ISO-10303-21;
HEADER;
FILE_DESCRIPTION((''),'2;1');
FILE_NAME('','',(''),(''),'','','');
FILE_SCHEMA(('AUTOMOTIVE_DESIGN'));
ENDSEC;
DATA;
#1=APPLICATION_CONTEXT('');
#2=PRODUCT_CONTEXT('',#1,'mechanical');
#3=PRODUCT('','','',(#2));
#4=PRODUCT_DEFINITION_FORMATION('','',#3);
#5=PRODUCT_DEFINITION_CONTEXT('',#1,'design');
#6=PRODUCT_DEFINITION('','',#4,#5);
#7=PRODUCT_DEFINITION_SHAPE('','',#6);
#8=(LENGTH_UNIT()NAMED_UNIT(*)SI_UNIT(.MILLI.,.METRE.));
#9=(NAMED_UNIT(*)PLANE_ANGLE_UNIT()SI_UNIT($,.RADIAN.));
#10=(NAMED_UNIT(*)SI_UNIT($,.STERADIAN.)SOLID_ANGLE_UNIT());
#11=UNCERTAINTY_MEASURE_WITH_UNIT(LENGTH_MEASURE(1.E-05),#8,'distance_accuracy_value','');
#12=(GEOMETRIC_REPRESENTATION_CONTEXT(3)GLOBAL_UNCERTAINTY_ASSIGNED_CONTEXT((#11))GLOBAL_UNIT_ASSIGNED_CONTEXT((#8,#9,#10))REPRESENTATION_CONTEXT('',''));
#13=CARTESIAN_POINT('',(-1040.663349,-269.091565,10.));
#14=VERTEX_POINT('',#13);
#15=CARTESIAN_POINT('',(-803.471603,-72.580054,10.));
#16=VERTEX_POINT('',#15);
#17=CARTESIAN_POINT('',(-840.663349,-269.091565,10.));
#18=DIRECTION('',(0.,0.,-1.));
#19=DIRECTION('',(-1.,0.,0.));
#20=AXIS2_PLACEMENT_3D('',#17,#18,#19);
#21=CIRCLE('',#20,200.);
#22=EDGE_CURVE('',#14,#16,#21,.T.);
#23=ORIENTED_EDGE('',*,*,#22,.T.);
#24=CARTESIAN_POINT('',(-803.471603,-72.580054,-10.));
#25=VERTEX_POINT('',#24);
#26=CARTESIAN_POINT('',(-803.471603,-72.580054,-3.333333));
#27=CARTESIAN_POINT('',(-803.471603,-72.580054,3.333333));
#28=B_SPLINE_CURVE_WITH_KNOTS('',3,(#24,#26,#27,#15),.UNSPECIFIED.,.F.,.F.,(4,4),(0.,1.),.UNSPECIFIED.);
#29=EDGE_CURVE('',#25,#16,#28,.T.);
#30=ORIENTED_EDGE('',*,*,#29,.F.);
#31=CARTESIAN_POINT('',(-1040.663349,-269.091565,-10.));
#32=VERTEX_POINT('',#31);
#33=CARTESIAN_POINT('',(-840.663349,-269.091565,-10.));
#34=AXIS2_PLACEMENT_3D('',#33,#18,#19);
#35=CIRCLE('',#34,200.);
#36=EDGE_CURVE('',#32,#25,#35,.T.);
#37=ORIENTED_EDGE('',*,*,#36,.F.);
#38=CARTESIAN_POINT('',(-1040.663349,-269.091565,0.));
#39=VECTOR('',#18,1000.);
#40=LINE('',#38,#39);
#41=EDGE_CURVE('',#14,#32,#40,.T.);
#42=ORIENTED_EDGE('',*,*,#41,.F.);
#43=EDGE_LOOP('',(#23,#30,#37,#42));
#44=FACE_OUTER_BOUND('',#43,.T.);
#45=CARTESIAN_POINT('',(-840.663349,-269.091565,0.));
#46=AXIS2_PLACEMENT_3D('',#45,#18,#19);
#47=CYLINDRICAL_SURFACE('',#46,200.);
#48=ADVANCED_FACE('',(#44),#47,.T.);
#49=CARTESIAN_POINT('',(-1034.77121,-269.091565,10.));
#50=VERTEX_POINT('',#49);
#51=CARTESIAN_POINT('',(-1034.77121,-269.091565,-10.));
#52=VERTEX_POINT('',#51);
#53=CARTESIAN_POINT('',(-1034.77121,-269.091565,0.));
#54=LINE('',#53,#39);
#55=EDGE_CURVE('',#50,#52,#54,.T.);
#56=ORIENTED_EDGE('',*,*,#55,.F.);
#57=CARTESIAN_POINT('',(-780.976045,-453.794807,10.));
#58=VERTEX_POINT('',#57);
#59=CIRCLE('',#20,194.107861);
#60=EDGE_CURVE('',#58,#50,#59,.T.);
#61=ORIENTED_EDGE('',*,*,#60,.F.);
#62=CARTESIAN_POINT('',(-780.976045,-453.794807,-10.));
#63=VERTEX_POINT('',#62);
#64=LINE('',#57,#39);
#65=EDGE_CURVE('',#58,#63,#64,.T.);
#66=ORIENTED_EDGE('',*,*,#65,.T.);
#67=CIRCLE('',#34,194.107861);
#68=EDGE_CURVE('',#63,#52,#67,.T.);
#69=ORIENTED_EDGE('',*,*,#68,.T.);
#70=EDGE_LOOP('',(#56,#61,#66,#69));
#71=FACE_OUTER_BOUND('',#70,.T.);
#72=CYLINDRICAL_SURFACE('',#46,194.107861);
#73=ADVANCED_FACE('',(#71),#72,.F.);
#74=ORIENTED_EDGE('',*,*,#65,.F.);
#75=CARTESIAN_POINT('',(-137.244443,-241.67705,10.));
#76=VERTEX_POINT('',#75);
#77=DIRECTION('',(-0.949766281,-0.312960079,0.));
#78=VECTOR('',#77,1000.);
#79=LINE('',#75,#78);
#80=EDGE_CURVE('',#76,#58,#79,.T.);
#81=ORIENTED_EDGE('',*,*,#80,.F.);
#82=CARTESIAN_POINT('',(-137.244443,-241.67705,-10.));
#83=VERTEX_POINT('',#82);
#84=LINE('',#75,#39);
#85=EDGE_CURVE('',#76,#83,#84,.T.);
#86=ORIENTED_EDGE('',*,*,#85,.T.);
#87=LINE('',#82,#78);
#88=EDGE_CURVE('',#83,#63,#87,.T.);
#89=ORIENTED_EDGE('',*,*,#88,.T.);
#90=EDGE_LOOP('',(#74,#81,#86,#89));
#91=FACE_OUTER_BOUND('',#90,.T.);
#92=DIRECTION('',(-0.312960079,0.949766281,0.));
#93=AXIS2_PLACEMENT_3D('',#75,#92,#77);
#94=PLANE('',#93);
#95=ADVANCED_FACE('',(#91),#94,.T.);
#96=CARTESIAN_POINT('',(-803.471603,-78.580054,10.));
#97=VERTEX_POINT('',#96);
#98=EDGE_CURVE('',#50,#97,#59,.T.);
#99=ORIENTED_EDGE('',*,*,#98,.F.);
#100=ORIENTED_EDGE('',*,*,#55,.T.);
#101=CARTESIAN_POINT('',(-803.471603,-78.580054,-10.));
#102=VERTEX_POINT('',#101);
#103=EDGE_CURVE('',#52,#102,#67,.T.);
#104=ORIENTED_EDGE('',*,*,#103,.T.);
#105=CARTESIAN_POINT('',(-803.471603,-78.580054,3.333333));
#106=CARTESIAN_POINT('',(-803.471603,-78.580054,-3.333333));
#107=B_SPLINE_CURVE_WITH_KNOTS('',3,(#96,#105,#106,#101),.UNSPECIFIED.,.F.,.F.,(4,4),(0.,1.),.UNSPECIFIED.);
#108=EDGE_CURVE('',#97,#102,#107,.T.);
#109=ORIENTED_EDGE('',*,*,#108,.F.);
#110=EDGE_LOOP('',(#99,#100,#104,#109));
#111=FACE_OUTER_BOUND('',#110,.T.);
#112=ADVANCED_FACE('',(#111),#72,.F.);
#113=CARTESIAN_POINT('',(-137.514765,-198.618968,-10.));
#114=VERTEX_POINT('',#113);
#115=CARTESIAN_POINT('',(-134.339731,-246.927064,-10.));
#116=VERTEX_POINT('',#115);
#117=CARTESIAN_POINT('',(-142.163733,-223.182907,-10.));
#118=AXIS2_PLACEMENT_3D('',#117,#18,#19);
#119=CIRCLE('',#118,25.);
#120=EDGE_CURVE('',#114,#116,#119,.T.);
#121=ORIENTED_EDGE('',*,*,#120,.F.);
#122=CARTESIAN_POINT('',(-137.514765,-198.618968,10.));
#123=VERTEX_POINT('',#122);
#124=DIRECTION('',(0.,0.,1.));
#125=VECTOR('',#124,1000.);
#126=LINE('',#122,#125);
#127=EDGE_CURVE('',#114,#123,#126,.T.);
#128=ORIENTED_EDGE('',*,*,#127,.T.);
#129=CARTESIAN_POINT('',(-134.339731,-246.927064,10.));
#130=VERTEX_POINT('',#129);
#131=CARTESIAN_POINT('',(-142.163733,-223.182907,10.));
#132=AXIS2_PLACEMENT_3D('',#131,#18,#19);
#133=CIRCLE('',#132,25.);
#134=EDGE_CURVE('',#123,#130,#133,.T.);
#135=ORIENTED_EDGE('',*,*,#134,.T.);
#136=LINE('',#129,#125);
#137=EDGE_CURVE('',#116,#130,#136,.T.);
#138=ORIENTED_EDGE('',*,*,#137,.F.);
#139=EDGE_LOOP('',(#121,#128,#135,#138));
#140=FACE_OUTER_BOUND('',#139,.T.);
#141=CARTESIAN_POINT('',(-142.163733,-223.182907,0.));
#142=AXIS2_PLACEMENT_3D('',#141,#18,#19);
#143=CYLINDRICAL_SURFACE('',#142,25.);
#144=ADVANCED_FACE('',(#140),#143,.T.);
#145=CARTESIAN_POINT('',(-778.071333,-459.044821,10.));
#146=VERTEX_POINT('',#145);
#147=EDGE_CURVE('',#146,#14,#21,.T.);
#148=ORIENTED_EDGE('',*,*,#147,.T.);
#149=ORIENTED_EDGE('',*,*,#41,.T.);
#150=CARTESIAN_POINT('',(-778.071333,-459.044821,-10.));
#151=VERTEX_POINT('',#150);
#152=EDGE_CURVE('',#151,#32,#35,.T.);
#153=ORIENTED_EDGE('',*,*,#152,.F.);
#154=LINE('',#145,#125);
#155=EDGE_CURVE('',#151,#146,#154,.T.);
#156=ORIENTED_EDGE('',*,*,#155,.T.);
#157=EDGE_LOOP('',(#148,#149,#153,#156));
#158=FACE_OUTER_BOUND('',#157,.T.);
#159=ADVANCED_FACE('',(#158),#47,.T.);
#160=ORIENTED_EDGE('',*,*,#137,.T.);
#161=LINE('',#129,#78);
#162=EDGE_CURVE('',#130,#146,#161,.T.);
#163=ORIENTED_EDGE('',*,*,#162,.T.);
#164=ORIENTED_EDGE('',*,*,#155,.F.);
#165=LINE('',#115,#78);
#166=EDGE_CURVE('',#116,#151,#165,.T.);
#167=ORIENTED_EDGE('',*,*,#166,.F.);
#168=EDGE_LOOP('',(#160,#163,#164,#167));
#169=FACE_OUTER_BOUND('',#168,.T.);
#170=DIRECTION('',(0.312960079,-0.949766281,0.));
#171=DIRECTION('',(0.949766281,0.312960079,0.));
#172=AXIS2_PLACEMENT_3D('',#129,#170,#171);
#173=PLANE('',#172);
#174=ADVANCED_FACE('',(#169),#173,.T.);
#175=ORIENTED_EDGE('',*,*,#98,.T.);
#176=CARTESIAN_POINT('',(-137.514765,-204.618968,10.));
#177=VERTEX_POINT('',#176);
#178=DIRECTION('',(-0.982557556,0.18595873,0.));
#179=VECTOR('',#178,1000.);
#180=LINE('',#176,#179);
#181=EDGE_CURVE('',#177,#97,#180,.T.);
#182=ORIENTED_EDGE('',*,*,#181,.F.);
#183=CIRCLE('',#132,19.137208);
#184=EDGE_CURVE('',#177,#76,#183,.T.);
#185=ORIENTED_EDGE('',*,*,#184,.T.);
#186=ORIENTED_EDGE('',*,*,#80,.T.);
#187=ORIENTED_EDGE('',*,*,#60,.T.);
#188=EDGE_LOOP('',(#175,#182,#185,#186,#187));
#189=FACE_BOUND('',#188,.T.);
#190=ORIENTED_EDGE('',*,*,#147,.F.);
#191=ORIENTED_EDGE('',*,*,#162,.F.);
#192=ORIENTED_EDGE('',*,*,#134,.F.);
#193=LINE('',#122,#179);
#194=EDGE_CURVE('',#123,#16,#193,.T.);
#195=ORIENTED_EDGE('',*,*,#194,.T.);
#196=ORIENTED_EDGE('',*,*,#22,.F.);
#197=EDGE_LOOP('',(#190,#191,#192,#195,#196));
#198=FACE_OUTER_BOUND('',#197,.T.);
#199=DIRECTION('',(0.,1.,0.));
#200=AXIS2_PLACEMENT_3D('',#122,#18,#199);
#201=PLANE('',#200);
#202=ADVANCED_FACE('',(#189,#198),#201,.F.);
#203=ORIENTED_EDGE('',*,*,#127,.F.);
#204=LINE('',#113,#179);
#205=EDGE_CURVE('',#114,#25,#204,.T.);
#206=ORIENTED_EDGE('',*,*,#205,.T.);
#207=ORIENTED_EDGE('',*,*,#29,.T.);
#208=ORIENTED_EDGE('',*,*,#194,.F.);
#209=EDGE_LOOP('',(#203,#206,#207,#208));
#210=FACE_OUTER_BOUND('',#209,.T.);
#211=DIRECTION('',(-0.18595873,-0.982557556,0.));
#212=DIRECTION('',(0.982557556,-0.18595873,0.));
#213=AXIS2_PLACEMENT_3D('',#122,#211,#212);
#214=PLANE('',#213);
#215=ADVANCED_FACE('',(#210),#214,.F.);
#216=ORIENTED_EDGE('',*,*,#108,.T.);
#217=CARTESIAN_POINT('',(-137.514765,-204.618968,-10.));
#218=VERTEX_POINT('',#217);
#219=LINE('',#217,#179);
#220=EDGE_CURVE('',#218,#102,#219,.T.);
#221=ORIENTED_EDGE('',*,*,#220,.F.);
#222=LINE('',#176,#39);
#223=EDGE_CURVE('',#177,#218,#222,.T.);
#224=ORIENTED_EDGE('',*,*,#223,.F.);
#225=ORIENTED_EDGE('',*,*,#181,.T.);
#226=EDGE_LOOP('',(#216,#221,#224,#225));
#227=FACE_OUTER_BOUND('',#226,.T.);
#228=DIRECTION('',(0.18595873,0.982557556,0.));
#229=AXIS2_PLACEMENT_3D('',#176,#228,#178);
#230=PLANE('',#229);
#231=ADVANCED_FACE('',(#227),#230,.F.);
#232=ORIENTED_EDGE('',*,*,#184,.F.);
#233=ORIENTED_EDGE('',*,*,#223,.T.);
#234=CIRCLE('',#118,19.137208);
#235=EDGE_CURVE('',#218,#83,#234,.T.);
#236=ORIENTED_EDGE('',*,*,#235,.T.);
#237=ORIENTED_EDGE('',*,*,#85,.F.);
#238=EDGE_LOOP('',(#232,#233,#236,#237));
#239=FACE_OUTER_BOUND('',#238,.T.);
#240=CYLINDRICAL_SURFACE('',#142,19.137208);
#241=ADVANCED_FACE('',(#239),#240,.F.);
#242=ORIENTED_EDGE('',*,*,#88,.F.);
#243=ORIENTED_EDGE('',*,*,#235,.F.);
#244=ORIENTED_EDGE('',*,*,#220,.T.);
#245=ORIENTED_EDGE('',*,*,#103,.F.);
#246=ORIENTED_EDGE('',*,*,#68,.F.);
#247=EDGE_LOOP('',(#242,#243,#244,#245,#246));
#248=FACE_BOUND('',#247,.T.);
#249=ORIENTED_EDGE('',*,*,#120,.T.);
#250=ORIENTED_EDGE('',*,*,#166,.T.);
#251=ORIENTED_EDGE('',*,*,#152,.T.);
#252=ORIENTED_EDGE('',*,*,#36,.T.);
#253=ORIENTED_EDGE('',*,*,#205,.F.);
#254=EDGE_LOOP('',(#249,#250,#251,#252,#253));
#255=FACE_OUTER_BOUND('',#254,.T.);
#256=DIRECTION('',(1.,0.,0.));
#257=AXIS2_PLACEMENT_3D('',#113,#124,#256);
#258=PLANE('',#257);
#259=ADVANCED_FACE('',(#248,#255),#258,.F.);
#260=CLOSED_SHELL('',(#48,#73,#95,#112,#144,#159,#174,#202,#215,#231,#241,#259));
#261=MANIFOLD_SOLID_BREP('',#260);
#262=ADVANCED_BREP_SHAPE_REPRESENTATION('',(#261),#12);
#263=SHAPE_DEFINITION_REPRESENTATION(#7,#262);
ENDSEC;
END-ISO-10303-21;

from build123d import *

# Parameters (mm, degrees)
SKETCH2_W = 20
SKETCH2_H = 6


with BuildPart() as part:
    # Sweep1: sweep along a path in Sketch1
    with BuildLine(Plane.XY) as sweep1_path:
        Line((-803.471602915, -72.580053696), (-137.514764545, -198.618968438))
        ThreePointArc((-137.514764545, -198.618968438), (-117.217555143, -221.543328014), (-134.339730828, -246.927064367))
        Line((-134.339730828, -246.927064367), (-778.071333179, -459.044821132))
        ThreePointArc((-778.071333179, -459.044821132), (-1040.232770199, -282.208199453), (-803.471602915, -72.580053696))
    # Sketch2 → Sweep1 (sweep)
    with BuildSketch(Plane(origin=(-803.471602915, 0, 0), x_dir=(0, 0, -1), z_dir=(1, 0, 0))):
        with Locations((0, -75.580053696)):
            Rectangle(SKETCH2_W, SKETCH2_H)
    sweep(path=sweep1_path.line)


solid = part.part
